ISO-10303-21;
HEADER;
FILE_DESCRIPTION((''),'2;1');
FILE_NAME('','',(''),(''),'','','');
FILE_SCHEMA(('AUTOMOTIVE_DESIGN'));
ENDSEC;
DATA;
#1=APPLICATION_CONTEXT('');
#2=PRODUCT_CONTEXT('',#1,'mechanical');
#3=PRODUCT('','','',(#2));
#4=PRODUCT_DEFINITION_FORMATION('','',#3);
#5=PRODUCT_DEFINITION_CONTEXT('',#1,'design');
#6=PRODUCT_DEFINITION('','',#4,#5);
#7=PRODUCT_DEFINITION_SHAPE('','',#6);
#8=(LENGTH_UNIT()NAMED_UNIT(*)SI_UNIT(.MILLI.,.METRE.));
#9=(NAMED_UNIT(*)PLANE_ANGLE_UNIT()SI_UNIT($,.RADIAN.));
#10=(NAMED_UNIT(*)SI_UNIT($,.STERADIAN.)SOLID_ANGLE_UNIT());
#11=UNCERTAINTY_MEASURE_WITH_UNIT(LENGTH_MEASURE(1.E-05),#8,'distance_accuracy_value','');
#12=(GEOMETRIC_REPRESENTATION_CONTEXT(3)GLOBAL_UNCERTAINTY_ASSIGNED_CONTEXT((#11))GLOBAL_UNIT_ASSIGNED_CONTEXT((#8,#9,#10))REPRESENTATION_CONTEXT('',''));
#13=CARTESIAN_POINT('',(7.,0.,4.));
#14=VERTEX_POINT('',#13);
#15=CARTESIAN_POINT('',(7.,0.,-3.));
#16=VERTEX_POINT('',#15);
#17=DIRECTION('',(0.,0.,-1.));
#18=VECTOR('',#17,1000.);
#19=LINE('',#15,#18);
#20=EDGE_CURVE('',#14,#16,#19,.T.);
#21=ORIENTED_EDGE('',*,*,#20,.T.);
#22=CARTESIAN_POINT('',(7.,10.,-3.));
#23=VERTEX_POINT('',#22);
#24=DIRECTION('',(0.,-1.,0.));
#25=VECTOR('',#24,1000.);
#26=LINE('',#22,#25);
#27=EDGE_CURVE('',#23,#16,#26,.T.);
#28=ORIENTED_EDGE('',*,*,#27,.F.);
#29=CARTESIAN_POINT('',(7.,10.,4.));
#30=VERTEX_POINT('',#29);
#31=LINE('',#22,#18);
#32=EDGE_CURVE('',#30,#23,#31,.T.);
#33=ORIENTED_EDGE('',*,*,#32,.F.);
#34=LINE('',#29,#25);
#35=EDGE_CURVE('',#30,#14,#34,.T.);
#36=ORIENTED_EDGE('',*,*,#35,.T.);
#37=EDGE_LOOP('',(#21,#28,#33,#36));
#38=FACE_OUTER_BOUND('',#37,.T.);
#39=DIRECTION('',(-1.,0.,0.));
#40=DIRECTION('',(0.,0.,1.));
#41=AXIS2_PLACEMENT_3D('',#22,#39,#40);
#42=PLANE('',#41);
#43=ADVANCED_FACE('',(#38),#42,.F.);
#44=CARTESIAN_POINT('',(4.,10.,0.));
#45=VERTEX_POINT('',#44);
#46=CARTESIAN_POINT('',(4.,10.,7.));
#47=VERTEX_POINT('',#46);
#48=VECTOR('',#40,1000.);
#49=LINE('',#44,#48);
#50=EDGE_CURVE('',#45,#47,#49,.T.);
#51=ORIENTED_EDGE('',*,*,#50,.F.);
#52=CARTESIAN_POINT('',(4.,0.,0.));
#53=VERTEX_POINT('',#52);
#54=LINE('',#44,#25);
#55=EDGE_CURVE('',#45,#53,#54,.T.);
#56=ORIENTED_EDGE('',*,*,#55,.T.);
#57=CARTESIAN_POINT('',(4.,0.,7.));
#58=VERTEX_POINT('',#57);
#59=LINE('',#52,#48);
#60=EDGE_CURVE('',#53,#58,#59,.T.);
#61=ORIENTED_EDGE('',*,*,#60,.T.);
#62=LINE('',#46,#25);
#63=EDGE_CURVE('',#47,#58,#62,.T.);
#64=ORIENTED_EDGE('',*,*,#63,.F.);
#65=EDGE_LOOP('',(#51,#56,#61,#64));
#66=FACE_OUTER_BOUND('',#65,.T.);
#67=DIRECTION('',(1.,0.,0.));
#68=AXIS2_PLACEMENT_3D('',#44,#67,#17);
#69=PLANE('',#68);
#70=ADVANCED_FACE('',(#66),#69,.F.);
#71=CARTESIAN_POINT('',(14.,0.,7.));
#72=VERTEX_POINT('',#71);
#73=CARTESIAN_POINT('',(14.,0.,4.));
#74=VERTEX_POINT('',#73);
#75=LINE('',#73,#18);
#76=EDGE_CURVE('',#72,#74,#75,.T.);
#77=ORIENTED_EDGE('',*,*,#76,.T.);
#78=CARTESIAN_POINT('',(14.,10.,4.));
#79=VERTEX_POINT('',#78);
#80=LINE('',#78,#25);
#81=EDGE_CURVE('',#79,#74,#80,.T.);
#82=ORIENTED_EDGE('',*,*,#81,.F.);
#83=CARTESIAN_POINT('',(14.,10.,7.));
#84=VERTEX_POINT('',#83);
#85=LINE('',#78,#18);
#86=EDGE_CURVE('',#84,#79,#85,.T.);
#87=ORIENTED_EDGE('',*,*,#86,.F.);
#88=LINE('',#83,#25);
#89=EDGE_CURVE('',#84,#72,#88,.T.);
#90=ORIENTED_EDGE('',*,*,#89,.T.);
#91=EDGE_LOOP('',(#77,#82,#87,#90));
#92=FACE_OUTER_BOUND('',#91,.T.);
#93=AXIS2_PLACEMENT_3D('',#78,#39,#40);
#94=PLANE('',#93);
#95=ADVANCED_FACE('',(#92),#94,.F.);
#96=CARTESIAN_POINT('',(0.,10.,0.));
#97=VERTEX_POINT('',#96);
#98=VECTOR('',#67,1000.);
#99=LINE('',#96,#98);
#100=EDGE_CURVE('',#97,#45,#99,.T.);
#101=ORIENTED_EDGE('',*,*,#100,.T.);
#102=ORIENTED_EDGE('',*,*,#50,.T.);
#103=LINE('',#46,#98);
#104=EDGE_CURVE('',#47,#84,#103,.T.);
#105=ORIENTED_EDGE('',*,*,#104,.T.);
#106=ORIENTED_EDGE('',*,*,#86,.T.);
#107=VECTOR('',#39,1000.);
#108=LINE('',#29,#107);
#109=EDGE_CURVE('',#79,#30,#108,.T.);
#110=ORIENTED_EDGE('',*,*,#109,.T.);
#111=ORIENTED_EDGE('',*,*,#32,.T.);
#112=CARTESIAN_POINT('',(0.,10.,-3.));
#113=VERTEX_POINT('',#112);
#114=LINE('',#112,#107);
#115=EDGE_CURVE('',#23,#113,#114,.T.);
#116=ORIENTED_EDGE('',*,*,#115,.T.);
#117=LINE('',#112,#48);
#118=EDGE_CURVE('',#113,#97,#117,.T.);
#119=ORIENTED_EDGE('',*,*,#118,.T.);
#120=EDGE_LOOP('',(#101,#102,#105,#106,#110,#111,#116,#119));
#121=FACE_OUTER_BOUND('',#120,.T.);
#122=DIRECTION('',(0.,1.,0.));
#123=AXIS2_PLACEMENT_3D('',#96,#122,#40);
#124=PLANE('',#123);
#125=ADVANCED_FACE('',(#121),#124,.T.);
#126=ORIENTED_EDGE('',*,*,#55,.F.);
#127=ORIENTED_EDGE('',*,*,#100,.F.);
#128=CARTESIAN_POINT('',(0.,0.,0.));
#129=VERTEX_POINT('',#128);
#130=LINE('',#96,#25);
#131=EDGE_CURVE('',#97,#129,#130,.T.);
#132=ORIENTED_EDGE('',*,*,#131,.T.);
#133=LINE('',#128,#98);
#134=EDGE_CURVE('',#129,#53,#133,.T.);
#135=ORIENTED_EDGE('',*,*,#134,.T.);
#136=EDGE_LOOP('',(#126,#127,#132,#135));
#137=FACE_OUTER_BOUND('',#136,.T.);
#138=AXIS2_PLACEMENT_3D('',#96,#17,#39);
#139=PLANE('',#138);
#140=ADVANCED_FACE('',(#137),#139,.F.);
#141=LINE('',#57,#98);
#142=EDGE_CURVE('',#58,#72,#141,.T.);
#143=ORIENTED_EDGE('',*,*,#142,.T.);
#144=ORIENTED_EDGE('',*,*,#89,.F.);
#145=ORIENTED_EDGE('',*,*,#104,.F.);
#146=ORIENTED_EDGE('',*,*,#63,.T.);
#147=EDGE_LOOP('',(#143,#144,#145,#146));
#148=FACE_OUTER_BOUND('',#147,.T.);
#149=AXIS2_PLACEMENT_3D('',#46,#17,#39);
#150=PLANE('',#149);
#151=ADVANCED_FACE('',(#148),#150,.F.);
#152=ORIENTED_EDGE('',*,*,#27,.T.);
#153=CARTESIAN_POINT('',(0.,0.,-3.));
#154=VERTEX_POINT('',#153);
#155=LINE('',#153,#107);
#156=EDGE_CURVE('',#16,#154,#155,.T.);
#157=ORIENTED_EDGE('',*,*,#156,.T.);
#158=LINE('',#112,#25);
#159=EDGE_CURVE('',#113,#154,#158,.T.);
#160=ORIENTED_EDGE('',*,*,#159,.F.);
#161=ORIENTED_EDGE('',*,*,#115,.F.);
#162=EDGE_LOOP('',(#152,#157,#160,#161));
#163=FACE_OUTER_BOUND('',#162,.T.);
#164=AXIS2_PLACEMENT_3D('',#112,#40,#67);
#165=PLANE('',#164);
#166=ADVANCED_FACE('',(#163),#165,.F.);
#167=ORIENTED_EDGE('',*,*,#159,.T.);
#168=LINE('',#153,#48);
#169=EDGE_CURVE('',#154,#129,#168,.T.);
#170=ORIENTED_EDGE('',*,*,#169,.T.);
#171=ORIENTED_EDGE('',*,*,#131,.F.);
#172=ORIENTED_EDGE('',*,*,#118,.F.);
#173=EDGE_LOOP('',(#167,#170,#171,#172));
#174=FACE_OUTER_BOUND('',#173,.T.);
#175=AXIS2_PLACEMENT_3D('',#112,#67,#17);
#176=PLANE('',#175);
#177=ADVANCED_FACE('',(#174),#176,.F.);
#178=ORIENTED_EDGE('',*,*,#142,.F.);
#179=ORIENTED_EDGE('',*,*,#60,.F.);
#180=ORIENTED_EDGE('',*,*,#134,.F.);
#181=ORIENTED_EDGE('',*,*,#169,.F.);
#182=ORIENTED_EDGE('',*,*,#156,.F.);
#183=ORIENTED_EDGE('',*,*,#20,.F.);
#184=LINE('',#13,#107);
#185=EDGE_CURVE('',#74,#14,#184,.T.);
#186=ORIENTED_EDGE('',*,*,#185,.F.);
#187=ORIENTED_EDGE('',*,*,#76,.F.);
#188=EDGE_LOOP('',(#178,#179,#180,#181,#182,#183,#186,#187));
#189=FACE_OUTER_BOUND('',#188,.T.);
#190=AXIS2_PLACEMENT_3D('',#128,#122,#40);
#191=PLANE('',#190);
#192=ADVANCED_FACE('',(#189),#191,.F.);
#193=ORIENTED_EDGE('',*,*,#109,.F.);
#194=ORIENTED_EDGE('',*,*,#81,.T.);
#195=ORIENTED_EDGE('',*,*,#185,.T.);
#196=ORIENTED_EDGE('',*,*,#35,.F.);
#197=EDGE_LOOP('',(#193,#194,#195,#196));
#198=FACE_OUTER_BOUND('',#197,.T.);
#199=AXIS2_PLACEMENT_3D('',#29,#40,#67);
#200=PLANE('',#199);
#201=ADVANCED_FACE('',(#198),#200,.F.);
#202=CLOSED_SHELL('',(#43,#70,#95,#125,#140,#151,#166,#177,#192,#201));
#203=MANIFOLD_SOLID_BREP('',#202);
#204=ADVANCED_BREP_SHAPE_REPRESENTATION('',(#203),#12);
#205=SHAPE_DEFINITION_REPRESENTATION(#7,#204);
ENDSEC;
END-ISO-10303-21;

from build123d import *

# Parameters (mm, degrees)
BOSS_EXTRUDE1_DEPTH = 10


with BuildPart() as part:
    # Sketch1 → Boss-Extrude1 (new body)
    with BuildSketch(Plane(origin=(0, 0, 0), x_dir=(1, 0, 0), z_dir=(0, 1, 0))):
        Polygon((0, 0), (4, 0), (4, -7), (14, -7), (14, -4), (7, -4), (7, 3), (0, 3), align=None)
    extrude(amount=BOSS_EXTRUDE1_DEPTH)


solid = part.part
